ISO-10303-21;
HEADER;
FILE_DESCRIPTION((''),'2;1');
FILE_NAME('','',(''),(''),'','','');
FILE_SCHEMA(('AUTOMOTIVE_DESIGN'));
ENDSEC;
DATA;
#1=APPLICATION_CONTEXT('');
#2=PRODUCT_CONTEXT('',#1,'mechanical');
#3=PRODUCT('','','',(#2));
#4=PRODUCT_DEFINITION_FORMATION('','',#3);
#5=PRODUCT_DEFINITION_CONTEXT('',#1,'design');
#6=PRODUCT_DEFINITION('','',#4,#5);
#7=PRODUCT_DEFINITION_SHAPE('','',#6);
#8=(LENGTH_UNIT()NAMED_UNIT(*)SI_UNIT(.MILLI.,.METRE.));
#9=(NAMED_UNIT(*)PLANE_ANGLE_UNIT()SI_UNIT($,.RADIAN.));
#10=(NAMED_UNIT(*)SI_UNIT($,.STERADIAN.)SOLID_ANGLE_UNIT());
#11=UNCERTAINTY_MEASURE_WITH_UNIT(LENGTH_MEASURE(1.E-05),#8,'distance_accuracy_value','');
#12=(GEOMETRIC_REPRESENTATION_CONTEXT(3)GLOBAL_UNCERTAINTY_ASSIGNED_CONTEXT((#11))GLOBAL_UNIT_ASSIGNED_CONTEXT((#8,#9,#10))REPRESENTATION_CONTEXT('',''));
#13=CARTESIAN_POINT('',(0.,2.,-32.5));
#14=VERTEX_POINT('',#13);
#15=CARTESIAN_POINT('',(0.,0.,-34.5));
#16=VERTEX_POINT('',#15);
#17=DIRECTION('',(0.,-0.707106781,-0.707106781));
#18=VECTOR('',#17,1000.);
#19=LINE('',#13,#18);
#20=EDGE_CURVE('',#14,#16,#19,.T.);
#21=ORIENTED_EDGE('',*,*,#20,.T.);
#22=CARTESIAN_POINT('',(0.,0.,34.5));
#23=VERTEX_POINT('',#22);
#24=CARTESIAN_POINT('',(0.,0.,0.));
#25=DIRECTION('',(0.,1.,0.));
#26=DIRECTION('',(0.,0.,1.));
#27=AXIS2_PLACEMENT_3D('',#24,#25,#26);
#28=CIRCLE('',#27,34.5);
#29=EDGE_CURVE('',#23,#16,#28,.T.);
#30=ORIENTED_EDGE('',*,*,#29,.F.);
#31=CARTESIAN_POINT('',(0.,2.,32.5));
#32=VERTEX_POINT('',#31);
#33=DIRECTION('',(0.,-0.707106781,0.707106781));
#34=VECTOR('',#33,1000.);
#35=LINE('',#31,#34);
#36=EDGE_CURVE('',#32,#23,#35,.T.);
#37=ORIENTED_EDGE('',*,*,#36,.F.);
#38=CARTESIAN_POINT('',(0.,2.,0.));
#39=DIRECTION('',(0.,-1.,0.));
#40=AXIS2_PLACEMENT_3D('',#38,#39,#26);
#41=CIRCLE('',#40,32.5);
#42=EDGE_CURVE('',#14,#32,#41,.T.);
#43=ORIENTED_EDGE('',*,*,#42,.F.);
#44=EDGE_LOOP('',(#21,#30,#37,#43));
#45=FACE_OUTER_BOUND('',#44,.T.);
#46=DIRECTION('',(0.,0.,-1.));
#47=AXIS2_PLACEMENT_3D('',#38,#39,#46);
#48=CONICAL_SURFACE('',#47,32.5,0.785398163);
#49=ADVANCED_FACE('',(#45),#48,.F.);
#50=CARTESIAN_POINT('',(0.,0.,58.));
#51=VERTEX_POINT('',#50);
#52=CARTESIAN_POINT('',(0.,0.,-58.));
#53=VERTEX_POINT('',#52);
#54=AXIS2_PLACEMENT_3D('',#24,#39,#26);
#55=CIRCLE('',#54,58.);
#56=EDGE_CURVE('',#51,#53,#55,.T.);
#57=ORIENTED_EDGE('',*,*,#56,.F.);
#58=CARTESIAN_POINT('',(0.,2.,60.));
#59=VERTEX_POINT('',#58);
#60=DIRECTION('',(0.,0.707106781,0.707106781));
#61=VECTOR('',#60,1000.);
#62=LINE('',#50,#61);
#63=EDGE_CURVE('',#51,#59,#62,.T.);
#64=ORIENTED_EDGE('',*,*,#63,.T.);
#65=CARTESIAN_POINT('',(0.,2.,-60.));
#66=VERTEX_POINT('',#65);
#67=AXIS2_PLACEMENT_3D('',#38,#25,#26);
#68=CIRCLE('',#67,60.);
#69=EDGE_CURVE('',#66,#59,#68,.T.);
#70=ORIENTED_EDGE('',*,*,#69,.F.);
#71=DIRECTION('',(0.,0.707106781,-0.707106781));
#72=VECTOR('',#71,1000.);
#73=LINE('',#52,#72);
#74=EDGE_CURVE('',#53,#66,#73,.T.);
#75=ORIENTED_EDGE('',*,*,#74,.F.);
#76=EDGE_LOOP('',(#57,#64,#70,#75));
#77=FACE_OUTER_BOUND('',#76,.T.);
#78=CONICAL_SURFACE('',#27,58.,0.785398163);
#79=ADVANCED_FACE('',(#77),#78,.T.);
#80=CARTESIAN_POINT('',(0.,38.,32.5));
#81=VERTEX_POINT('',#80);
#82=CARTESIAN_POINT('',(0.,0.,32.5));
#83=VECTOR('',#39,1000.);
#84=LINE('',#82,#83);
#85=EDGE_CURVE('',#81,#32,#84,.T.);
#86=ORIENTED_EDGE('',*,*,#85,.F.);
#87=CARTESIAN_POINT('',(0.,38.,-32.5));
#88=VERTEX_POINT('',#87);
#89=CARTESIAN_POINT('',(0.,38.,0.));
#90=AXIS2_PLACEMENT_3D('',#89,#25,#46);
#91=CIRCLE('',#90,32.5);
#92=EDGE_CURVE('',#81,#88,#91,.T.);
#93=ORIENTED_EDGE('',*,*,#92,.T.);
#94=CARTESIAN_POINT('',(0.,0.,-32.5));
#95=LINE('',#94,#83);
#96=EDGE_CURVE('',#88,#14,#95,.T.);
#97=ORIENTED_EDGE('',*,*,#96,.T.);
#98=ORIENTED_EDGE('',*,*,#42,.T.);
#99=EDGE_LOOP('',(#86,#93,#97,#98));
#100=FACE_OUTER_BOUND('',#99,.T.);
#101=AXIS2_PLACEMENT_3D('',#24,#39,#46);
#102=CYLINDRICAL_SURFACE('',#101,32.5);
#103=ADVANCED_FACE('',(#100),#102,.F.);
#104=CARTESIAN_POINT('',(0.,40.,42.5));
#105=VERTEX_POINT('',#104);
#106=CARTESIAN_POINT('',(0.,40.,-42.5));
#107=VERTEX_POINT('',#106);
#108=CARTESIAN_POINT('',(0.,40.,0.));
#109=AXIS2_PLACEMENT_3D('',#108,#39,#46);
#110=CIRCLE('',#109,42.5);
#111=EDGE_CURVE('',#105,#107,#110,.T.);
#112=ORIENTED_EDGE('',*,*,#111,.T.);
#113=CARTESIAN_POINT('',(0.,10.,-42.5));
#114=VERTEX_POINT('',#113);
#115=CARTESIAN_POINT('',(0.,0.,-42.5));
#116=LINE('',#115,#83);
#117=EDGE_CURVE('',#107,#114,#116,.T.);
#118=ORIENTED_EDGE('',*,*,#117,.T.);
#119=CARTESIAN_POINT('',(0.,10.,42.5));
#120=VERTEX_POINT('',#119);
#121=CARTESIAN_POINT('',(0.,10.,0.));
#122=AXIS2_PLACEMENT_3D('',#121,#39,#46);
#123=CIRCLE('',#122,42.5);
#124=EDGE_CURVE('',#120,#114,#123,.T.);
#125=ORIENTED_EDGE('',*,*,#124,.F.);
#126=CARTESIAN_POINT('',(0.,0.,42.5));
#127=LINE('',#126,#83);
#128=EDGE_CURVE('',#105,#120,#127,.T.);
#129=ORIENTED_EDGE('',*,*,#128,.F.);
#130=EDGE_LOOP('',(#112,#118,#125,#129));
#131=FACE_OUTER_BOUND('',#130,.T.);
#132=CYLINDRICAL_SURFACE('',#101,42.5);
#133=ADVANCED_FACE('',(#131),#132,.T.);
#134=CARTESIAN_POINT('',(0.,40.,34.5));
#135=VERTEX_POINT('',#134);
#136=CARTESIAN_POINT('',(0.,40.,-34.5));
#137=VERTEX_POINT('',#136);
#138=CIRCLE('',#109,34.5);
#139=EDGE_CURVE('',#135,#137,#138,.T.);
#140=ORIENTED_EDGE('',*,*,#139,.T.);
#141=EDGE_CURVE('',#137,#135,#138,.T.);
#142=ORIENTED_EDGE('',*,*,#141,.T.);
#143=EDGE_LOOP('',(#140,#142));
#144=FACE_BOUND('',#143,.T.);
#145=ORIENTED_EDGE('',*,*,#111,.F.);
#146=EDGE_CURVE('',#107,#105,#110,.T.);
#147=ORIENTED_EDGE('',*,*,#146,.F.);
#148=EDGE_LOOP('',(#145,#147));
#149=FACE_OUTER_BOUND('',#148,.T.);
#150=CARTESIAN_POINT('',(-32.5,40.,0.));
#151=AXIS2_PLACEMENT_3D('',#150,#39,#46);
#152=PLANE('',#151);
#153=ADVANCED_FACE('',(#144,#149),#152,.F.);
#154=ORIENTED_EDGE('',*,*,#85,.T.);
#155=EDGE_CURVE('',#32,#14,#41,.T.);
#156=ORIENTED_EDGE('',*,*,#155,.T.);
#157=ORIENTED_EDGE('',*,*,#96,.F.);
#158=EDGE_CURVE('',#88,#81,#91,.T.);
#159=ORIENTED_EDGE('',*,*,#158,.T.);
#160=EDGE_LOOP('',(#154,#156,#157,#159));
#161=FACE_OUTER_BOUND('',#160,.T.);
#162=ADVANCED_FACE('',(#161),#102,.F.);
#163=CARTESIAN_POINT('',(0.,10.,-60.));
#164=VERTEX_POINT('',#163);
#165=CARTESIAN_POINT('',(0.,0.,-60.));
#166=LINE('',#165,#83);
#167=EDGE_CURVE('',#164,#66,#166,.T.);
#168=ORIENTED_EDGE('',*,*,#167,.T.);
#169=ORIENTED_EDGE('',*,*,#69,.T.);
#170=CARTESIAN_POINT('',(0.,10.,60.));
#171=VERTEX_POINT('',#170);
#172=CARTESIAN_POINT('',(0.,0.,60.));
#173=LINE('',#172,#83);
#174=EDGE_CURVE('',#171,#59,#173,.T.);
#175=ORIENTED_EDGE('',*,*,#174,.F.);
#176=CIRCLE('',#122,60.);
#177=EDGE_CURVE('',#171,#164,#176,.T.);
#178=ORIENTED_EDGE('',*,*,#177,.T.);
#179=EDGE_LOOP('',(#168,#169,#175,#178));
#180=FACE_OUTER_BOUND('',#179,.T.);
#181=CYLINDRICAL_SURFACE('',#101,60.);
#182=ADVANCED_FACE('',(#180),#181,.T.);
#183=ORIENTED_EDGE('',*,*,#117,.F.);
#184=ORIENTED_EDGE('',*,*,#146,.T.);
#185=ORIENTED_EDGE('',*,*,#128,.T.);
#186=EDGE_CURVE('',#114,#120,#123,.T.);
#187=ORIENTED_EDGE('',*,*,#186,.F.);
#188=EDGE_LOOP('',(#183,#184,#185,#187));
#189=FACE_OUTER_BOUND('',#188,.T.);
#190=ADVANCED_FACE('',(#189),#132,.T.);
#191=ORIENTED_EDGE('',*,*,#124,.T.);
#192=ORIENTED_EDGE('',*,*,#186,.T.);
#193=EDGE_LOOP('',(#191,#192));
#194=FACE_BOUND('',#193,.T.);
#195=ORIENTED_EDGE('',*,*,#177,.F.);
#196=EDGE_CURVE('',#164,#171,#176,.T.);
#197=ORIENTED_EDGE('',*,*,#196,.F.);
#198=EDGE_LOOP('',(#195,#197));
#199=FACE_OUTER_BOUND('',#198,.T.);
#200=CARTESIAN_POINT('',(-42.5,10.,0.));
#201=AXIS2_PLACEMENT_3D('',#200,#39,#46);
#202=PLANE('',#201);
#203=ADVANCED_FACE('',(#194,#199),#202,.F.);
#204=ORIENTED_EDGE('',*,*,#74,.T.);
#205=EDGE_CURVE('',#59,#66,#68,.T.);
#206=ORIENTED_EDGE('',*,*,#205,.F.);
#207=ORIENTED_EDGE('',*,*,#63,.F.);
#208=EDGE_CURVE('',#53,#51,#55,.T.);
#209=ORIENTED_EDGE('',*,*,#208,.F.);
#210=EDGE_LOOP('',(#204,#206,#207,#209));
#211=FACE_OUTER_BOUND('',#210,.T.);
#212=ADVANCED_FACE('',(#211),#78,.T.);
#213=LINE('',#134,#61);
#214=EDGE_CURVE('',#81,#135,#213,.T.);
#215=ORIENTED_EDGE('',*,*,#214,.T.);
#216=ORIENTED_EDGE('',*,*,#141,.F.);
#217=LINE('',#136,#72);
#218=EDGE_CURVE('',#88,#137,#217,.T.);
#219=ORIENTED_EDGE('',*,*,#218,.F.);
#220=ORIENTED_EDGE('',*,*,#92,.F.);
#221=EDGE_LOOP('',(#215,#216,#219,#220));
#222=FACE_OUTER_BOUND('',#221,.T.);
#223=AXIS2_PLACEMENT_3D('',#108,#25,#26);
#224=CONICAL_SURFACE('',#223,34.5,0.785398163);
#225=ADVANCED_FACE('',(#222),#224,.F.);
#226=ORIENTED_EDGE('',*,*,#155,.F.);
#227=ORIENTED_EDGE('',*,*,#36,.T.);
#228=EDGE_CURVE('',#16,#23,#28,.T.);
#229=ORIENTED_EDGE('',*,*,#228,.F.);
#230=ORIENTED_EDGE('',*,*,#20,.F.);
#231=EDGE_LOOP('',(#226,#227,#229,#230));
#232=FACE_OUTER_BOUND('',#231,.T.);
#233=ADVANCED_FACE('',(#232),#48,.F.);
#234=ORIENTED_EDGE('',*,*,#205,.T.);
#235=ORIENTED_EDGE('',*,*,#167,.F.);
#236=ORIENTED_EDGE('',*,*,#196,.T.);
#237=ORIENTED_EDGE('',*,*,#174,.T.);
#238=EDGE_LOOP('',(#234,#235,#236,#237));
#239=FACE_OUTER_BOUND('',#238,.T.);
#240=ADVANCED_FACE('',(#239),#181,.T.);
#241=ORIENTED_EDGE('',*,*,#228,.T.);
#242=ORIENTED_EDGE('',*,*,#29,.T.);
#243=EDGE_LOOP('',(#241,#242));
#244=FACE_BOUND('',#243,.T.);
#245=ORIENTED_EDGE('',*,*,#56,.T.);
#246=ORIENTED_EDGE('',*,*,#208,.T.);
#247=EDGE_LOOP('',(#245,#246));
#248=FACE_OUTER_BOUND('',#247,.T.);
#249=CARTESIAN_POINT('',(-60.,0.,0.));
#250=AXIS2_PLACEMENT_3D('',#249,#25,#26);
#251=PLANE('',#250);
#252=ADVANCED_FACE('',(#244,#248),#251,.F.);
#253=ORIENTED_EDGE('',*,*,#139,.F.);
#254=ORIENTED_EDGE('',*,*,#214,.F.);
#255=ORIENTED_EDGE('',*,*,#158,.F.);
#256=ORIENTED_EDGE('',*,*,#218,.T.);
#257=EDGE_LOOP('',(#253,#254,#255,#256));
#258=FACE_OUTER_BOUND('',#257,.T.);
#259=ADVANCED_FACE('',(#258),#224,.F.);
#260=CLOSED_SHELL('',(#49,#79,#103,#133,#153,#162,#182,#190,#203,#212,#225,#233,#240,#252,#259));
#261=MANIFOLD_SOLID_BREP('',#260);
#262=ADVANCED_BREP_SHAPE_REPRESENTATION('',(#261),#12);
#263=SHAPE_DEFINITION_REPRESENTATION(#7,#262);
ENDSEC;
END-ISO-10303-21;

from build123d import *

# Parameters (mm, degrees)
CHAMFER1_SIZE = 2


with BuildPart() as part:
    # Sketch1 → Revolve1 (revolve)
    with BuildSketch(Plane.XY, mode=Mode.PRIVATE) as revolve1_sk:
        Polygon((-32.5, 0), (-32.5, 40), (-42.5, 40), (-42.5, 10), (-60, 10), (-60, 0), align=None)
    revolve(revolve1_sk.sketch.rotate(Axis((0, 0, 0), (0, 1, 0)), 270), axis=Axis((0, 0, 0), (0, 1, 0)))

    # Chamfer1
    chamfer1_edges = [part.edges().sort_by_distance(p)[0] for p in [
        (0, 0, 60),
        (0, 40, 32.5),
        (0, 0, 32.5),
    ]]
    chamfer(chamfer1_edges, length=CHAMFER1_SIZE)


solid = part.part
